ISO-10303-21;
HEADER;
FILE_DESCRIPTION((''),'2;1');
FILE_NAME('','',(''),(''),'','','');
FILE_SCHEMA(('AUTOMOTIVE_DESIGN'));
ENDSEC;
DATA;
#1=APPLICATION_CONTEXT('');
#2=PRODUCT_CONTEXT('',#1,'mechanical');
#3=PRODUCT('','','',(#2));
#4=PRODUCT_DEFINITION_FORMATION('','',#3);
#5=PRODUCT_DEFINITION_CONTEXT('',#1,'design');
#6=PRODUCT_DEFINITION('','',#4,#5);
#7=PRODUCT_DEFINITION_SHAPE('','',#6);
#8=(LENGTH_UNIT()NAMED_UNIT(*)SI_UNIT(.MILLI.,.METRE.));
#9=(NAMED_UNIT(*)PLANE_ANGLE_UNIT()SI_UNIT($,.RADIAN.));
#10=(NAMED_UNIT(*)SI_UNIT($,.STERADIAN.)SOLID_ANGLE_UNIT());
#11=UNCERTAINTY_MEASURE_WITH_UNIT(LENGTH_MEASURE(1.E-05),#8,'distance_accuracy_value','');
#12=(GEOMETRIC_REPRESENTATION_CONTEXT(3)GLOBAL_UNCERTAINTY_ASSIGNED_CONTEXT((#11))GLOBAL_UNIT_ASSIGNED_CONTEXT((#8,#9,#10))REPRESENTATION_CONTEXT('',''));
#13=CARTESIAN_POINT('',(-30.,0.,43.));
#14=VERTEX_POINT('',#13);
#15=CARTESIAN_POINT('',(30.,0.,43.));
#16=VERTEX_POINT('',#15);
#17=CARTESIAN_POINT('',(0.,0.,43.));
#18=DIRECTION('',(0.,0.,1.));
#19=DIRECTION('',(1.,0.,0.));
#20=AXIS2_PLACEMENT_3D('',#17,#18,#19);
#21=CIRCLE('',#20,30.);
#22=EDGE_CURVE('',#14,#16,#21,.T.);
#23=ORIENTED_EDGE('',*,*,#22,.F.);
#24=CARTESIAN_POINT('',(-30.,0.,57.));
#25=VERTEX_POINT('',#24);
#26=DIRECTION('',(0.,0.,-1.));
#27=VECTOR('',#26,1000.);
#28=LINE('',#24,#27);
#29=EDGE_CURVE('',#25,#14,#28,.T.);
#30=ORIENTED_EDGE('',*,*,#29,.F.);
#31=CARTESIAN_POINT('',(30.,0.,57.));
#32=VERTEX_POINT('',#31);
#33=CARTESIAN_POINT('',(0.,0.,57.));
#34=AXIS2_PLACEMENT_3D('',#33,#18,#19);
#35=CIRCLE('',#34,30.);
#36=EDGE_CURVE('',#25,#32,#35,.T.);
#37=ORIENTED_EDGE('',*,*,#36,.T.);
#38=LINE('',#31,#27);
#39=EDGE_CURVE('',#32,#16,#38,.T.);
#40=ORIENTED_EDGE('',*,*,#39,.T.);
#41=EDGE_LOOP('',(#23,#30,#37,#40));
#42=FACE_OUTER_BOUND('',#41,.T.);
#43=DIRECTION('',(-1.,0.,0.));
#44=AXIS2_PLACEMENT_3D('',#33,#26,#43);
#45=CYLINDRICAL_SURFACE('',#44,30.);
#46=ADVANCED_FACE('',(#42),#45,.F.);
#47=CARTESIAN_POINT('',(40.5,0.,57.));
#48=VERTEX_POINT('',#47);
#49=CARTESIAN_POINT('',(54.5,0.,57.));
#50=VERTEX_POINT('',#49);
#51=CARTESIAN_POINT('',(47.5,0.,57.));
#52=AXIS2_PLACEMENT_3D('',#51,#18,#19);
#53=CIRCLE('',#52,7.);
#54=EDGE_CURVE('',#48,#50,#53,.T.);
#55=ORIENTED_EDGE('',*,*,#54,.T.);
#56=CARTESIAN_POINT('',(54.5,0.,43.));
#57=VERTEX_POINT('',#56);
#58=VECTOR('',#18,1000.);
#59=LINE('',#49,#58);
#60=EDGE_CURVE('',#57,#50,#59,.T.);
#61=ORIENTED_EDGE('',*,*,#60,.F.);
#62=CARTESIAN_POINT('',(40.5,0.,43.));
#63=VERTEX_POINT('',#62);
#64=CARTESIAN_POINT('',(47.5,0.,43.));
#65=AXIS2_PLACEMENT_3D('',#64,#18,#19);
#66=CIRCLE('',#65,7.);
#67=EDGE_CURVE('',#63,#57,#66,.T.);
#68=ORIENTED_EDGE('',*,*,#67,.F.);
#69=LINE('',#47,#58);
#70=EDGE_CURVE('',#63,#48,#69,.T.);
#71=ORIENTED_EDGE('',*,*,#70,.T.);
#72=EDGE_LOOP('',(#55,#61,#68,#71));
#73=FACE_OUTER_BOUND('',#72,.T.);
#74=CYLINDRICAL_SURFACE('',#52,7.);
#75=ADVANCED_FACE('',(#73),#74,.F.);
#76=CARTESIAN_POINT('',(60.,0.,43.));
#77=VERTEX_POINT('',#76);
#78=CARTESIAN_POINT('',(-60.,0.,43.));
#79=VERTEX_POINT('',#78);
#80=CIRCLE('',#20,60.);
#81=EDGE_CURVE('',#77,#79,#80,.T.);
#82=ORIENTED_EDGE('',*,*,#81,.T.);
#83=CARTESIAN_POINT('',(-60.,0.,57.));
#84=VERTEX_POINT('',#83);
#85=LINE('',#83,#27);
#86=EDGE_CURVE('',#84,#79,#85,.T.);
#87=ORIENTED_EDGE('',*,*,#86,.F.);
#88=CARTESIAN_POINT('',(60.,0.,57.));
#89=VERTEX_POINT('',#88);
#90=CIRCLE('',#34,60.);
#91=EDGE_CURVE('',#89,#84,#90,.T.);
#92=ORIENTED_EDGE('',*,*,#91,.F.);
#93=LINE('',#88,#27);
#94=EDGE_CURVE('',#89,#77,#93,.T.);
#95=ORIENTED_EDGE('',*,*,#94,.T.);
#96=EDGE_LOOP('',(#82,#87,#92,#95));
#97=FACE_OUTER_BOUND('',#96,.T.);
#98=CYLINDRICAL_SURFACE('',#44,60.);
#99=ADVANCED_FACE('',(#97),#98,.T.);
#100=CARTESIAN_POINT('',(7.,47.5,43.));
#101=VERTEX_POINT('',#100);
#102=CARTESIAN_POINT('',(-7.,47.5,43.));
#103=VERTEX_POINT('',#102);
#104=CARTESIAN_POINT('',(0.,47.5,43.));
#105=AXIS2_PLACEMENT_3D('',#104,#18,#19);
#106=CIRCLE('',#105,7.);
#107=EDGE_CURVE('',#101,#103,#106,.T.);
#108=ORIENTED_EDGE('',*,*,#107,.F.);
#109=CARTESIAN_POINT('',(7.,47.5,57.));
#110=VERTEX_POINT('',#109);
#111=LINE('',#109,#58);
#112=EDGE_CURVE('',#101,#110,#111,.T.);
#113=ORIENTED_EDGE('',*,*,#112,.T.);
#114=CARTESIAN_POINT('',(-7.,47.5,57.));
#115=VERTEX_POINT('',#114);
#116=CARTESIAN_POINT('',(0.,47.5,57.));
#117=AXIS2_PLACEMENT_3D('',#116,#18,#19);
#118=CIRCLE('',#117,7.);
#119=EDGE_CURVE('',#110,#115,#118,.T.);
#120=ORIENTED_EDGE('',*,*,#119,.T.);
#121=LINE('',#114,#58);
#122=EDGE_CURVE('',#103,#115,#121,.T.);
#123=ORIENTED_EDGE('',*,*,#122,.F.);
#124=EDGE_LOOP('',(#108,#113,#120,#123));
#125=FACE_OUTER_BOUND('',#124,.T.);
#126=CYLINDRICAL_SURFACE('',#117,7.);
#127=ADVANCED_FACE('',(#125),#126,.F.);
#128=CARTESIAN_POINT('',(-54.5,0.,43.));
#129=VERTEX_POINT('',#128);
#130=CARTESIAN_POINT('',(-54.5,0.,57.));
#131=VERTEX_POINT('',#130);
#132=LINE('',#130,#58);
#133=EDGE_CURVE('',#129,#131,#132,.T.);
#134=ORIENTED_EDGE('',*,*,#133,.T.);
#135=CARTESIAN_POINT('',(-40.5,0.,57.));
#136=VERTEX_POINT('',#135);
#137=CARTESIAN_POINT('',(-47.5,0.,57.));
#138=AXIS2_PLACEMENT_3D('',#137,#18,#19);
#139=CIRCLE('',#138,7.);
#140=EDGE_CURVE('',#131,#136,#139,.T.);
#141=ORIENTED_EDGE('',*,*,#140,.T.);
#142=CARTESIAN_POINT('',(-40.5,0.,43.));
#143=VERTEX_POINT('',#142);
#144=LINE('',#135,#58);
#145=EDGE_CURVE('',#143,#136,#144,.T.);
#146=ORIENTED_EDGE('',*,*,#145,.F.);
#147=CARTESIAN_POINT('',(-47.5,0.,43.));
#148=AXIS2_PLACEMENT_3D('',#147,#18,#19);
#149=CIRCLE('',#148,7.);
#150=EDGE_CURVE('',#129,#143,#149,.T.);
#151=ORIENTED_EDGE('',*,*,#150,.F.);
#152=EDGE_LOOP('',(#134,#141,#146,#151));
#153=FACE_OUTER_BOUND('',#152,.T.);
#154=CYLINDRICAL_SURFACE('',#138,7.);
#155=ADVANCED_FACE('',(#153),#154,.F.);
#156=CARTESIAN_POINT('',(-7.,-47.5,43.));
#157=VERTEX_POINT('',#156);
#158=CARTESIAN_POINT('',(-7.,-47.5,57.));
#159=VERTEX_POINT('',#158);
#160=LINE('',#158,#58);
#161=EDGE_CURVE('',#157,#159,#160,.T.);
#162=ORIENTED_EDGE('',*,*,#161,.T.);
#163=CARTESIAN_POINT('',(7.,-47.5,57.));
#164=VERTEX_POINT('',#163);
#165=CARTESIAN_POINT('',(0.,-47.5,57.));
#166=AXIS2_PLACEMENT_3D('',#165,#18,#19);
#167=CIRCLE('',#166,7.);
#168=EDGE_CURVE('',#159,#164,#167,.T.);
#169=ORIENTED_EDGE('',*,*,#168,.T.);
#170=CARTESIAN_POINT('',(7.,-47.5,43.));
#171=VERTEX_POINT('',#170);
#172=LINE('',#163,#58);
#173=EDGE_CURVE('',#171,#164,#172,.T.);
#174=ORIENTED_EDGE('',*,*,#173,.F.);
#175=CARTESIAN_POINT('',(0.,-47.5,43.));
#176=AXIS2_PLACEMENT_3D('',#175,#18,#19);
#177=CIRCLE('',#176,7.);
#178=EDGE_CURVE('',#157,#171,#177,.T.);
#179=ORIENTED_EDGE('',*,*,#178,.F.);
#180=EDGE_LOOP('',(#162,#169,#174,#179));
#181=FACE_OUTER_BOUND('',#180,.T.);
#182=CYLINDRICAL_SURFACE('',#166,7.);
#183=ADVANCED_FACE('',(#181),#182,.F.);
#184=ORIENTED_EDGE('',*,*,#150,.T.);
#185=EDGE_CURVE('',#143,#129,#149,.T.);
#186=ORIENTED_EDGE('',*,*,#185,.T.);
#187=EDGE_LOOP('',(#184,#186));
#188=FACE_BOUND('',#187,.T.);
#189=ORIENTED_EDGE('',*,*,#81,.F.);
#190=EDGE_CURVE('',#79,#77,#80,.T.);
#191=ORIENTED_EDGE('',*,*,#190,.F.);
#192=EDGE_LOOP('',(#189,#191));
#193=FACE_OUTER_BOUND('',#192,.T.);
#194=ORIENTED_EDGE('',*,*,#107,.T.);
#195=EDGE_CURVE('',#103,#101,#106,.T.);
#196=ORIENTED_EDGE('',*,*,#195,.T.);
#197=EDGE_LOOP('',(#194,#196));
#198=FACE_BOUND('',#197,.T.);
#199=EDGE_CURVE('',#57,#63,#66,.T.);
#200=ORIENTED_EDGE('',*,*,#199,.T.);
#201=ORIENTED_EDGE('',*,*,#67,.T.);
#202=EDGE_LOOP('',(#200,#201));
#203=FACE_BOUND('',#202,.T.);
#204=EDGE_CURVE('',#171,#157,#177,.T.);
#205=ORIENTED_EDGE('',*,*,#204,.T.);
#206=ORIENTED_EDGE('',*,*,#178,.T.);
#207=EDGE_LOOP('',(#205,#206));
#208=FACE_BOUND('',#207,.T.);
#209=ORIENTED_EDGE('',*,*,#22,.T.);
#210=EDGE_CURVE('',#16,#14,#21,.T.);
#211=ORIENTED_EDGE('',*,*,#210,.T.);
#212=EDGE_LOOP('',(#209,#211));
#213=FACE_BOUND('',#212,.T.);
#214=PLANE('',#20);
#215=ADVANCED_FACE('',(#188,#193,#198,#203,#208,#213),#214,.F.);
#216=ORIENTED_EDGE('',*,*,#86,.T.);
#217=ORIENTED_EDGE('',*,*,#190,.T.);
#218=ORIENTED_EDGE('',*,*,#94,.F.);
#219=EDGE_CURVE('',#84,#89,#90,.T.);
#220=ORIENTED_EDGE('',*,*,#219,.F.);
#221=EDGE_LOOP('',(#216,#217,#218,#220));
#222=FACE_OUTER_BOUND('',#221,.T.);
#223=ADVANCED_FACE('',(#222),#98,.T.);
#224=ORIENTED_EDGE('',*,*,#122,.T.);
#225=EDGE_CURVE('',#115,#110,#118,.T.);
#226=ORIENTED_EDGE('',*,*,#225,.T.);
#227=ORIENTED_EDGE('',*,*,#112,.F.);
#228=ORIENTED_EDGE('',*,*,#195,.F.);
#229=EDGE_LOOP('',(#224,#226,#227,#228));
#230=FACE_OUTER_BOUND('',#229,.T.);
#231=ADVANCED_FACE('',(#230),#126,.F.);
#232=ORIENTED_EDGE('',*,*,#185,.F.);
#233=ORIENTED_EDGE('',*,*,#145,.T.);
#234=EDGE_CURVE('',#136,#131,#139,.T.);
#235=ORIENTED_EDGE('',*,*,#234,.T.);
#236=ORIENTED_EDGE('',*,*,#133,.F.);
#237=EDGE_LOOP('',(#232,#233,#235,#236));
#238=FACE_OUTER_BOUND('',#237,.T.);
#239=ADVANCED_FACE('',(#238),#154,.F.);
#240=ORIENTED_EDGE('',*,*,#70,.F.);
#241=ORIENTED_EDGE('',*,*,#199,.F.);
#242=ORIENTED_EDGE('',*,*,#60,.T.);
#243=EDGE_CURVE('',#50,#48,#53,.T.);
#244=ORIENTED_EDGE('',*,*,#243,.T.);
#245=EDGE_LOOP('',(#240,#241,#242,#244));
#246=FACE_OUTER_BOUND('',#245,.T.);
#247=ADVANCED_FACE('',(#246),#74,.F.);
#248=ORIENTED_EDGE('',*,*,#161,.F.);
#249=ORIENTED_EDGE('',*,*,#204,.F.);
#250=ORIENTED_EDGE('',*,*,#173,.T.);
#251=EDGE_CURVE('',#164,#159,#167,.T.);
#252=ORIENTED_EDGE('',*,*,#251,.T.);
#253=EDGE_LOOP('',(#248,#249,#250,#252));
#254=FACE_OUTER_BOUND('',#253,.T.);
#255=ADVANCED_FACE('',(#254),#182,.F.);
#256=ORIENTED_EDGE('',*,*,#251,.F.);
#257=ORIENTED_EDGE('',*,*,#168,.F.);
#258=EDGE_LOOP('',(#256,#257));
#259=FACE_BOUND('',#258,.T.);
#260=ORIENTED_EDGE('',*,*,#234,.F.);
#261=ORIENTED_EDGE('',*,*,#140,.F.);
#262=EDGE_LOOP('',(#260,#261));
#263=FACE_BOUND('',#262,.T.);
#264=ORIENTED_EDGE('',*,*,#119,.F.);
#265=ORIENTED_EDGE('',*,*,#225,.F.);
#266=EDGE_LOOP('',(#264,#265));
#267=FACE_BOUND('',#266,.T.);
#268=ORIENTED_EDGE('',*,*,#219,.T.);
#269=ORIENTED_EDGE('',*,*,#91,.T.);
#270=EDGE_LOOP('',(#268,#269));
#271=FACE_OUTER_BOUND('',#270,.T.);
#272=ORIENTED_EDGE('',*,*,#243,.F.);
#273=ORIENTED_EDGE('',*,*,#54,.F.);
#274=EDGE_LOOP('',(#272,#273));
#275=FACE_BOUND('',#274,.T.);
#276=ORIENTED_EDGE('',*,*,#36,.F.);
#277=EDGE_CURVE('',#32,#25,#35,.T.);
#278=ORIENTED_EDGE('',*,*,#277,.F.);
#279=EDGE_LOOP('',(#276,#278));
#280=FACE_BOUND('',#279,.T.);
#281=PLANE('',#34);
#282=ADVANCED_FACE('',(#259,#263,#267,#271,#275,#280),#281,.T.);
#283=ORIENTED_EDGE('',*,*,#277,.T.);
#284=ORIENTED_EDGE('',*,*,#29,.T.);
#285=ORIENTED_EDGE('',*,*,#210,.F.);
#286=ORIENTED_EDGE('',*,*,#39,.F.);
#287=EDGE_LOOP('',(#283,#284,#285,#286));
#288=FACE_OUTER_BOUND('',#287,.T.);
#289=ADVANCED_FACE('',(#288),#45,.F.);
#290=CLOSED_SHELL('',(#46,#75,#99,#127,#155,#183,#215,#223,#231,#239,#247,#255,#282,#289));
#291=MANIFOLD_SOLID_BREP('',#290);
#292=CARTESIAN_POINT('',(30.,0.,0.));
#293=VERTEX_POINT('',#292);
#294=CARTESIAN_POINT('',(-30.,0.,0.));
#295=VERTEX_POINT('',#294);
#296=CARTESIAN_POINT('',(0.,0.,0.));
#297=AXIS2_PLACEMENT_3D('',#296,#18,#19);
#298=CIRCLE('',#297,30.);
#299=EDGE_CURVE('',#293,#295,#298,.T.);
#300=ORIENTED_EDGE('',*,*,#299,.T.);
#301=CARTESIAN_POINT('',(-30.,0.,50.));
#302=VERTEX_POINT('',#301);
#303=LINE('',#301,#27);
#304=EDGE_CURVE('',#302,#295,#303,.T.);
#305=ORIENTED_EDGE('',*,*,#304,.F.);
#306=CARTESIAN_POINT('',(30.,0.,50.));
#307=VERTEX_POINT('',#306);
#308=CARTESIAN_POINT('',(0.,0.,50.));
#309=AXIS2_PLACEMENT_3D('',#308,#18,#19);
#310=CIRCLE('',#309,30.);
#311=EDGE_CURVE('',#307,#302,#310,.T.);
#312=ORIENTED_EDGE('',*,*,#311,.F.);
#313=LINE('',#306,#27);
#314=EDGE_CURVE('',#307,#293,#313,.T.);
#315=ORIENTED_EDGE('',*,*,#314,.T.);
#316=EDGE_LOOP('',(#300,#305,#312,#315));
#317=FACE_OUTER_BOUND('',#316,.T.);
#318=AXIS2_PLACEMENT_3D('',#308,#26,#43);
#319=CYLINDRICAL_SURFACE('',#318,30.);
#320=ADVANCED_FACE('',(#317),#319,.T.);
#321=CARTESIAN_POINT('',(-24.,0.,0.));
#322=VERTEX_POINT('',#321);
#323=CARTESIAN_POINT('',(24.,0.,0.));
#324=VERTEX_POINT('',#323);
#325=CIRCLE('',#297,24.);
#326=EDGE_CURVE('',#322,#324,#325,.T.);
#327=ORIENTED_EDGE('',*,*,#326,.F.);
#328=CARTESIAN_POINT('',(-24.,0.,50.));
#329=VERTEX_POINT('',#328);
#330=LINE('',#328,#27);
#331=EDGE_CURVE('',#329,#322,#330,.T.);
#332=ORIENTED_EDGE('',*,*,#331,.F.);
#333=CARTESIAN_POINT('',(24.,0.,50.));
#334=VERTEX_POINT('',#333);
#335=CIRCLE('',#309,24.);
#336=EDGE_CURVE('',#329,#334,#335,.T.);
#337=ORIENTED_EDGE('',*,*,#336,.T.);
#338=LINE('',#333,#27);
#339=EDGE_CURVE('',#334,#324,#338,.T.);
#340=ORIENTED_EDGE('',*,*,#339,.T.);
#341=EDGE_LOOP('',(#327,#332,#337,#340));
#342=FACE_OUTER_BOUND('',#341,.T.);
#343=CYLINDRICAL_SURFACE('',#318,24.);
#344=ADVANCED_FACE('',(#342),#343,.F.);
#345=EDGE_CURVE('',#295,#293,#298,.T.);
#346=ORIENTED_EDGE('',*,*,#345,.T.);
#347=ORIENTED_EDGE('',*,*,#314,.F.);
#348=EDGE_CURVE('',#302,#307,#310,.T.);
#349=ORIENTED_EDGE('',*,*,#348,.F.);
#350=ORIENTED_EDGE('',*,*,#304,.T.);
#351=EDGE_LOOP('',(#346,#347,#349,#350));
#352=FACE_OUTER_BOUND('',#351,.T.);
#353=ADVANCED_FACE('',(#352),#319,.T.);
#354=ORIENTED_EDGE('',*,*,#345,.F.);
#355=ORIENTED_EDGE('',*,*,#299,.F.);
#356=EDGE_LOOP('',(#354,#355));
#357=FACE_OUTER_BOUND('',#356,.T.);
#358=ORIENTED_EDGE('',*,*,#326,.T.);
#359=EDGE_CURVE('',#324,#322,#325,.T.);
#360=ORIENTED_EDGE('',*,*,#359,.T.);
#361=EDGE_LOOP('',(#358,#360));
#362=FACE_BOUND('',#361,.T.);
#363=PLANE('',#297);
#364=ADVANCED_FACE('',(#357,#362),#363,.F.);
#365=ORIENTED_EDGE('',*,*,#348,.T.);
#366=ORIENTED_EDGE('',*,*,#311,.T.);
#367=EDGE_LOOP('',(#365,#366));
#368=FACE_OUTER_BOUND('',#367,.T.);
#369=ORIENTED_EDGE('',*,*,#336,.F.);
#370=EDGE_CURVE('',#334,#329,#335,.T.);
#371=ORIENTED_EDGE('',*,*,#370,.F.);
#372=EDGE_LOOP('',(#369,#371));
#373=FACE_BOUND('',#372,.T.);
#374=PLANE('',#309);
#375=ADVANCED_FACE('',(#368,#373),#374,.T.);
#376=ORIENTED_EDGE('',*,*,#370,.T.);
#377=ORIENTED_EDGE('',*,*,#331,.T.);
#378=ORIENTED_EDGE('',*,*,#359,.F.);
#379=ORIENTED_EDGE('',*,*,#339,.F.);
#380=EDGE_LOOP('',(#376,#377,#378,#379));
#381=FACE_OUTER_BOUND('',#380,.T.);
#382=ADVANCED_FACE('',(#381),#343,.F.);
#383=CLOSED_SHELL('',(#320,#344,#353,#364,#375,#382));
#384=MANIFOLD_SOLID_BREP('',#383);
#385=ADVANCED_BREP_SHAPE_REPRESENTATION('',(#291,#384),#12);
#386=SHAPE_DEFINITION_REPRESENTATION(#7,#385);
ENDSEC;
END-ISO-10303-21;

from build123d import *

# Parameters (mm, degrees)
SKETCH1_R                           = 30
SKETCH1_R_2                         = 24
EXTRUDE_THIN1_DEPTH                 = 50
SKETCH2_R                           = 60
SKETCH2_R_2                         = 30
BOSS_EXTRUDE1_DEPTH                 = 7
SKETCH4_W                           = 7
SKETCH4_H                           = 14.001
F_14_0_14_DIAMETER_HOLE1_AT_2_COUNT = 2
F_14_0_14_DIAMETER_HOLE1_AT_2_PITCH = 67.175144213
F_14_0_14_DIAMETER_HOLE1_AT_3_COUNT = 2
F_14_0_14_DIAMETER_HOLE1_AT_3_PITCH = 67.175144213
F_14_0_14_DIAMETER_HOLE1_AT_4_COUNT = 2
F_14_0_14_DIAMETER_HOLE1_AT_4_PITCH = 95


with BuildPart() as part:
    # Sketch1 → Extrude-Thin1 (new body)
    with BuildSketch(Plane.XY):
        Circle(SKETCH1_R)
        Circle(SKETCH1_R_2, mode=Mode.SUBTRACT)
    extrude(amount=EXTRUDE_THIN1_DEPTH)


with BuildPart() as body_2:
    # Sketch2 → Boss-Extrude1 (new, symmetric)
    with BuildSketch(Plane.XY.offset(50)):
        Circle(SKETCH2_R)
        Circle(SKETCH2_R_2, mode=Mode.SUBTRACT)
    extrude(amount=BOSS_EXTRUDE1_DEPTH, both=True)

    # Sketch4 → Ø14.0 (14) Diameter Hole1 (revolve, cut)
    with BuildSketch(Plane(origin=(0, 47.5, 57), x_dir=(0, -1, 0), z_dir=(1, 0, 0))):
        with Locations((3.5, 7.0005)):
            Rectangle(SKETCH4_W, SKETCH4_H)
    f_14_0_14_diameter_hole1 = revolve(axis=Axis((0, 47.5, 63.35), (0, 0, -1)), mode=Mode.SUBTRACT)

    # Ø14.0 (14) Diameter Hole1 at 2: Ø14.0 (14) Diameter Hole1 ×2
    with Locations(*[Vector(-0.7071067811865476, -0.7071067811865476, 0) * (i * F_14_0_14_DIAMETER_HOLE1_AT_2_PITCH) for i in range(1, F_14_0_14_DIAMETER_HOLE1_AT_2_COUNT)]):
        add(f_14_0_14_diameter_hole1, mode=Mode.SUBTRACT)

    # Ø14.0 (14) Diameter Hole1 at 3: Ø14.0 (14) Diameter Hole1 ×2
    with Locations(*[Vector(0.7071067811865476, -0.7071067811865476, 0) * (i * F_14_0_14_DIAMETER_HOLE1_AT_3_PITCH) for i in range(1, F_14_0_14_DIAMETER_HOLE1_AT_3_COUNT)]):
        add(f_14_0_14_diameter_hole1, mode=Mode.SUBTRACT)

    # Ø14.0 (14) Diameter Hole1 at 4: Ø14.0 (14) Diameter Hole1 ×2
    with Locations(*[(0, -i * F_14_0_14_DIAMETER_HOLE1_AT_4_PITCH, 0) for i in range(1, F_14_0_14_DIAMETER_HOLE1_AT_4_COUNT)]):
        add(f_14_0_14_diameter_hole1, mode=Mode.SUBTRACT)


solid = Compound([part.part, body_2.part])
